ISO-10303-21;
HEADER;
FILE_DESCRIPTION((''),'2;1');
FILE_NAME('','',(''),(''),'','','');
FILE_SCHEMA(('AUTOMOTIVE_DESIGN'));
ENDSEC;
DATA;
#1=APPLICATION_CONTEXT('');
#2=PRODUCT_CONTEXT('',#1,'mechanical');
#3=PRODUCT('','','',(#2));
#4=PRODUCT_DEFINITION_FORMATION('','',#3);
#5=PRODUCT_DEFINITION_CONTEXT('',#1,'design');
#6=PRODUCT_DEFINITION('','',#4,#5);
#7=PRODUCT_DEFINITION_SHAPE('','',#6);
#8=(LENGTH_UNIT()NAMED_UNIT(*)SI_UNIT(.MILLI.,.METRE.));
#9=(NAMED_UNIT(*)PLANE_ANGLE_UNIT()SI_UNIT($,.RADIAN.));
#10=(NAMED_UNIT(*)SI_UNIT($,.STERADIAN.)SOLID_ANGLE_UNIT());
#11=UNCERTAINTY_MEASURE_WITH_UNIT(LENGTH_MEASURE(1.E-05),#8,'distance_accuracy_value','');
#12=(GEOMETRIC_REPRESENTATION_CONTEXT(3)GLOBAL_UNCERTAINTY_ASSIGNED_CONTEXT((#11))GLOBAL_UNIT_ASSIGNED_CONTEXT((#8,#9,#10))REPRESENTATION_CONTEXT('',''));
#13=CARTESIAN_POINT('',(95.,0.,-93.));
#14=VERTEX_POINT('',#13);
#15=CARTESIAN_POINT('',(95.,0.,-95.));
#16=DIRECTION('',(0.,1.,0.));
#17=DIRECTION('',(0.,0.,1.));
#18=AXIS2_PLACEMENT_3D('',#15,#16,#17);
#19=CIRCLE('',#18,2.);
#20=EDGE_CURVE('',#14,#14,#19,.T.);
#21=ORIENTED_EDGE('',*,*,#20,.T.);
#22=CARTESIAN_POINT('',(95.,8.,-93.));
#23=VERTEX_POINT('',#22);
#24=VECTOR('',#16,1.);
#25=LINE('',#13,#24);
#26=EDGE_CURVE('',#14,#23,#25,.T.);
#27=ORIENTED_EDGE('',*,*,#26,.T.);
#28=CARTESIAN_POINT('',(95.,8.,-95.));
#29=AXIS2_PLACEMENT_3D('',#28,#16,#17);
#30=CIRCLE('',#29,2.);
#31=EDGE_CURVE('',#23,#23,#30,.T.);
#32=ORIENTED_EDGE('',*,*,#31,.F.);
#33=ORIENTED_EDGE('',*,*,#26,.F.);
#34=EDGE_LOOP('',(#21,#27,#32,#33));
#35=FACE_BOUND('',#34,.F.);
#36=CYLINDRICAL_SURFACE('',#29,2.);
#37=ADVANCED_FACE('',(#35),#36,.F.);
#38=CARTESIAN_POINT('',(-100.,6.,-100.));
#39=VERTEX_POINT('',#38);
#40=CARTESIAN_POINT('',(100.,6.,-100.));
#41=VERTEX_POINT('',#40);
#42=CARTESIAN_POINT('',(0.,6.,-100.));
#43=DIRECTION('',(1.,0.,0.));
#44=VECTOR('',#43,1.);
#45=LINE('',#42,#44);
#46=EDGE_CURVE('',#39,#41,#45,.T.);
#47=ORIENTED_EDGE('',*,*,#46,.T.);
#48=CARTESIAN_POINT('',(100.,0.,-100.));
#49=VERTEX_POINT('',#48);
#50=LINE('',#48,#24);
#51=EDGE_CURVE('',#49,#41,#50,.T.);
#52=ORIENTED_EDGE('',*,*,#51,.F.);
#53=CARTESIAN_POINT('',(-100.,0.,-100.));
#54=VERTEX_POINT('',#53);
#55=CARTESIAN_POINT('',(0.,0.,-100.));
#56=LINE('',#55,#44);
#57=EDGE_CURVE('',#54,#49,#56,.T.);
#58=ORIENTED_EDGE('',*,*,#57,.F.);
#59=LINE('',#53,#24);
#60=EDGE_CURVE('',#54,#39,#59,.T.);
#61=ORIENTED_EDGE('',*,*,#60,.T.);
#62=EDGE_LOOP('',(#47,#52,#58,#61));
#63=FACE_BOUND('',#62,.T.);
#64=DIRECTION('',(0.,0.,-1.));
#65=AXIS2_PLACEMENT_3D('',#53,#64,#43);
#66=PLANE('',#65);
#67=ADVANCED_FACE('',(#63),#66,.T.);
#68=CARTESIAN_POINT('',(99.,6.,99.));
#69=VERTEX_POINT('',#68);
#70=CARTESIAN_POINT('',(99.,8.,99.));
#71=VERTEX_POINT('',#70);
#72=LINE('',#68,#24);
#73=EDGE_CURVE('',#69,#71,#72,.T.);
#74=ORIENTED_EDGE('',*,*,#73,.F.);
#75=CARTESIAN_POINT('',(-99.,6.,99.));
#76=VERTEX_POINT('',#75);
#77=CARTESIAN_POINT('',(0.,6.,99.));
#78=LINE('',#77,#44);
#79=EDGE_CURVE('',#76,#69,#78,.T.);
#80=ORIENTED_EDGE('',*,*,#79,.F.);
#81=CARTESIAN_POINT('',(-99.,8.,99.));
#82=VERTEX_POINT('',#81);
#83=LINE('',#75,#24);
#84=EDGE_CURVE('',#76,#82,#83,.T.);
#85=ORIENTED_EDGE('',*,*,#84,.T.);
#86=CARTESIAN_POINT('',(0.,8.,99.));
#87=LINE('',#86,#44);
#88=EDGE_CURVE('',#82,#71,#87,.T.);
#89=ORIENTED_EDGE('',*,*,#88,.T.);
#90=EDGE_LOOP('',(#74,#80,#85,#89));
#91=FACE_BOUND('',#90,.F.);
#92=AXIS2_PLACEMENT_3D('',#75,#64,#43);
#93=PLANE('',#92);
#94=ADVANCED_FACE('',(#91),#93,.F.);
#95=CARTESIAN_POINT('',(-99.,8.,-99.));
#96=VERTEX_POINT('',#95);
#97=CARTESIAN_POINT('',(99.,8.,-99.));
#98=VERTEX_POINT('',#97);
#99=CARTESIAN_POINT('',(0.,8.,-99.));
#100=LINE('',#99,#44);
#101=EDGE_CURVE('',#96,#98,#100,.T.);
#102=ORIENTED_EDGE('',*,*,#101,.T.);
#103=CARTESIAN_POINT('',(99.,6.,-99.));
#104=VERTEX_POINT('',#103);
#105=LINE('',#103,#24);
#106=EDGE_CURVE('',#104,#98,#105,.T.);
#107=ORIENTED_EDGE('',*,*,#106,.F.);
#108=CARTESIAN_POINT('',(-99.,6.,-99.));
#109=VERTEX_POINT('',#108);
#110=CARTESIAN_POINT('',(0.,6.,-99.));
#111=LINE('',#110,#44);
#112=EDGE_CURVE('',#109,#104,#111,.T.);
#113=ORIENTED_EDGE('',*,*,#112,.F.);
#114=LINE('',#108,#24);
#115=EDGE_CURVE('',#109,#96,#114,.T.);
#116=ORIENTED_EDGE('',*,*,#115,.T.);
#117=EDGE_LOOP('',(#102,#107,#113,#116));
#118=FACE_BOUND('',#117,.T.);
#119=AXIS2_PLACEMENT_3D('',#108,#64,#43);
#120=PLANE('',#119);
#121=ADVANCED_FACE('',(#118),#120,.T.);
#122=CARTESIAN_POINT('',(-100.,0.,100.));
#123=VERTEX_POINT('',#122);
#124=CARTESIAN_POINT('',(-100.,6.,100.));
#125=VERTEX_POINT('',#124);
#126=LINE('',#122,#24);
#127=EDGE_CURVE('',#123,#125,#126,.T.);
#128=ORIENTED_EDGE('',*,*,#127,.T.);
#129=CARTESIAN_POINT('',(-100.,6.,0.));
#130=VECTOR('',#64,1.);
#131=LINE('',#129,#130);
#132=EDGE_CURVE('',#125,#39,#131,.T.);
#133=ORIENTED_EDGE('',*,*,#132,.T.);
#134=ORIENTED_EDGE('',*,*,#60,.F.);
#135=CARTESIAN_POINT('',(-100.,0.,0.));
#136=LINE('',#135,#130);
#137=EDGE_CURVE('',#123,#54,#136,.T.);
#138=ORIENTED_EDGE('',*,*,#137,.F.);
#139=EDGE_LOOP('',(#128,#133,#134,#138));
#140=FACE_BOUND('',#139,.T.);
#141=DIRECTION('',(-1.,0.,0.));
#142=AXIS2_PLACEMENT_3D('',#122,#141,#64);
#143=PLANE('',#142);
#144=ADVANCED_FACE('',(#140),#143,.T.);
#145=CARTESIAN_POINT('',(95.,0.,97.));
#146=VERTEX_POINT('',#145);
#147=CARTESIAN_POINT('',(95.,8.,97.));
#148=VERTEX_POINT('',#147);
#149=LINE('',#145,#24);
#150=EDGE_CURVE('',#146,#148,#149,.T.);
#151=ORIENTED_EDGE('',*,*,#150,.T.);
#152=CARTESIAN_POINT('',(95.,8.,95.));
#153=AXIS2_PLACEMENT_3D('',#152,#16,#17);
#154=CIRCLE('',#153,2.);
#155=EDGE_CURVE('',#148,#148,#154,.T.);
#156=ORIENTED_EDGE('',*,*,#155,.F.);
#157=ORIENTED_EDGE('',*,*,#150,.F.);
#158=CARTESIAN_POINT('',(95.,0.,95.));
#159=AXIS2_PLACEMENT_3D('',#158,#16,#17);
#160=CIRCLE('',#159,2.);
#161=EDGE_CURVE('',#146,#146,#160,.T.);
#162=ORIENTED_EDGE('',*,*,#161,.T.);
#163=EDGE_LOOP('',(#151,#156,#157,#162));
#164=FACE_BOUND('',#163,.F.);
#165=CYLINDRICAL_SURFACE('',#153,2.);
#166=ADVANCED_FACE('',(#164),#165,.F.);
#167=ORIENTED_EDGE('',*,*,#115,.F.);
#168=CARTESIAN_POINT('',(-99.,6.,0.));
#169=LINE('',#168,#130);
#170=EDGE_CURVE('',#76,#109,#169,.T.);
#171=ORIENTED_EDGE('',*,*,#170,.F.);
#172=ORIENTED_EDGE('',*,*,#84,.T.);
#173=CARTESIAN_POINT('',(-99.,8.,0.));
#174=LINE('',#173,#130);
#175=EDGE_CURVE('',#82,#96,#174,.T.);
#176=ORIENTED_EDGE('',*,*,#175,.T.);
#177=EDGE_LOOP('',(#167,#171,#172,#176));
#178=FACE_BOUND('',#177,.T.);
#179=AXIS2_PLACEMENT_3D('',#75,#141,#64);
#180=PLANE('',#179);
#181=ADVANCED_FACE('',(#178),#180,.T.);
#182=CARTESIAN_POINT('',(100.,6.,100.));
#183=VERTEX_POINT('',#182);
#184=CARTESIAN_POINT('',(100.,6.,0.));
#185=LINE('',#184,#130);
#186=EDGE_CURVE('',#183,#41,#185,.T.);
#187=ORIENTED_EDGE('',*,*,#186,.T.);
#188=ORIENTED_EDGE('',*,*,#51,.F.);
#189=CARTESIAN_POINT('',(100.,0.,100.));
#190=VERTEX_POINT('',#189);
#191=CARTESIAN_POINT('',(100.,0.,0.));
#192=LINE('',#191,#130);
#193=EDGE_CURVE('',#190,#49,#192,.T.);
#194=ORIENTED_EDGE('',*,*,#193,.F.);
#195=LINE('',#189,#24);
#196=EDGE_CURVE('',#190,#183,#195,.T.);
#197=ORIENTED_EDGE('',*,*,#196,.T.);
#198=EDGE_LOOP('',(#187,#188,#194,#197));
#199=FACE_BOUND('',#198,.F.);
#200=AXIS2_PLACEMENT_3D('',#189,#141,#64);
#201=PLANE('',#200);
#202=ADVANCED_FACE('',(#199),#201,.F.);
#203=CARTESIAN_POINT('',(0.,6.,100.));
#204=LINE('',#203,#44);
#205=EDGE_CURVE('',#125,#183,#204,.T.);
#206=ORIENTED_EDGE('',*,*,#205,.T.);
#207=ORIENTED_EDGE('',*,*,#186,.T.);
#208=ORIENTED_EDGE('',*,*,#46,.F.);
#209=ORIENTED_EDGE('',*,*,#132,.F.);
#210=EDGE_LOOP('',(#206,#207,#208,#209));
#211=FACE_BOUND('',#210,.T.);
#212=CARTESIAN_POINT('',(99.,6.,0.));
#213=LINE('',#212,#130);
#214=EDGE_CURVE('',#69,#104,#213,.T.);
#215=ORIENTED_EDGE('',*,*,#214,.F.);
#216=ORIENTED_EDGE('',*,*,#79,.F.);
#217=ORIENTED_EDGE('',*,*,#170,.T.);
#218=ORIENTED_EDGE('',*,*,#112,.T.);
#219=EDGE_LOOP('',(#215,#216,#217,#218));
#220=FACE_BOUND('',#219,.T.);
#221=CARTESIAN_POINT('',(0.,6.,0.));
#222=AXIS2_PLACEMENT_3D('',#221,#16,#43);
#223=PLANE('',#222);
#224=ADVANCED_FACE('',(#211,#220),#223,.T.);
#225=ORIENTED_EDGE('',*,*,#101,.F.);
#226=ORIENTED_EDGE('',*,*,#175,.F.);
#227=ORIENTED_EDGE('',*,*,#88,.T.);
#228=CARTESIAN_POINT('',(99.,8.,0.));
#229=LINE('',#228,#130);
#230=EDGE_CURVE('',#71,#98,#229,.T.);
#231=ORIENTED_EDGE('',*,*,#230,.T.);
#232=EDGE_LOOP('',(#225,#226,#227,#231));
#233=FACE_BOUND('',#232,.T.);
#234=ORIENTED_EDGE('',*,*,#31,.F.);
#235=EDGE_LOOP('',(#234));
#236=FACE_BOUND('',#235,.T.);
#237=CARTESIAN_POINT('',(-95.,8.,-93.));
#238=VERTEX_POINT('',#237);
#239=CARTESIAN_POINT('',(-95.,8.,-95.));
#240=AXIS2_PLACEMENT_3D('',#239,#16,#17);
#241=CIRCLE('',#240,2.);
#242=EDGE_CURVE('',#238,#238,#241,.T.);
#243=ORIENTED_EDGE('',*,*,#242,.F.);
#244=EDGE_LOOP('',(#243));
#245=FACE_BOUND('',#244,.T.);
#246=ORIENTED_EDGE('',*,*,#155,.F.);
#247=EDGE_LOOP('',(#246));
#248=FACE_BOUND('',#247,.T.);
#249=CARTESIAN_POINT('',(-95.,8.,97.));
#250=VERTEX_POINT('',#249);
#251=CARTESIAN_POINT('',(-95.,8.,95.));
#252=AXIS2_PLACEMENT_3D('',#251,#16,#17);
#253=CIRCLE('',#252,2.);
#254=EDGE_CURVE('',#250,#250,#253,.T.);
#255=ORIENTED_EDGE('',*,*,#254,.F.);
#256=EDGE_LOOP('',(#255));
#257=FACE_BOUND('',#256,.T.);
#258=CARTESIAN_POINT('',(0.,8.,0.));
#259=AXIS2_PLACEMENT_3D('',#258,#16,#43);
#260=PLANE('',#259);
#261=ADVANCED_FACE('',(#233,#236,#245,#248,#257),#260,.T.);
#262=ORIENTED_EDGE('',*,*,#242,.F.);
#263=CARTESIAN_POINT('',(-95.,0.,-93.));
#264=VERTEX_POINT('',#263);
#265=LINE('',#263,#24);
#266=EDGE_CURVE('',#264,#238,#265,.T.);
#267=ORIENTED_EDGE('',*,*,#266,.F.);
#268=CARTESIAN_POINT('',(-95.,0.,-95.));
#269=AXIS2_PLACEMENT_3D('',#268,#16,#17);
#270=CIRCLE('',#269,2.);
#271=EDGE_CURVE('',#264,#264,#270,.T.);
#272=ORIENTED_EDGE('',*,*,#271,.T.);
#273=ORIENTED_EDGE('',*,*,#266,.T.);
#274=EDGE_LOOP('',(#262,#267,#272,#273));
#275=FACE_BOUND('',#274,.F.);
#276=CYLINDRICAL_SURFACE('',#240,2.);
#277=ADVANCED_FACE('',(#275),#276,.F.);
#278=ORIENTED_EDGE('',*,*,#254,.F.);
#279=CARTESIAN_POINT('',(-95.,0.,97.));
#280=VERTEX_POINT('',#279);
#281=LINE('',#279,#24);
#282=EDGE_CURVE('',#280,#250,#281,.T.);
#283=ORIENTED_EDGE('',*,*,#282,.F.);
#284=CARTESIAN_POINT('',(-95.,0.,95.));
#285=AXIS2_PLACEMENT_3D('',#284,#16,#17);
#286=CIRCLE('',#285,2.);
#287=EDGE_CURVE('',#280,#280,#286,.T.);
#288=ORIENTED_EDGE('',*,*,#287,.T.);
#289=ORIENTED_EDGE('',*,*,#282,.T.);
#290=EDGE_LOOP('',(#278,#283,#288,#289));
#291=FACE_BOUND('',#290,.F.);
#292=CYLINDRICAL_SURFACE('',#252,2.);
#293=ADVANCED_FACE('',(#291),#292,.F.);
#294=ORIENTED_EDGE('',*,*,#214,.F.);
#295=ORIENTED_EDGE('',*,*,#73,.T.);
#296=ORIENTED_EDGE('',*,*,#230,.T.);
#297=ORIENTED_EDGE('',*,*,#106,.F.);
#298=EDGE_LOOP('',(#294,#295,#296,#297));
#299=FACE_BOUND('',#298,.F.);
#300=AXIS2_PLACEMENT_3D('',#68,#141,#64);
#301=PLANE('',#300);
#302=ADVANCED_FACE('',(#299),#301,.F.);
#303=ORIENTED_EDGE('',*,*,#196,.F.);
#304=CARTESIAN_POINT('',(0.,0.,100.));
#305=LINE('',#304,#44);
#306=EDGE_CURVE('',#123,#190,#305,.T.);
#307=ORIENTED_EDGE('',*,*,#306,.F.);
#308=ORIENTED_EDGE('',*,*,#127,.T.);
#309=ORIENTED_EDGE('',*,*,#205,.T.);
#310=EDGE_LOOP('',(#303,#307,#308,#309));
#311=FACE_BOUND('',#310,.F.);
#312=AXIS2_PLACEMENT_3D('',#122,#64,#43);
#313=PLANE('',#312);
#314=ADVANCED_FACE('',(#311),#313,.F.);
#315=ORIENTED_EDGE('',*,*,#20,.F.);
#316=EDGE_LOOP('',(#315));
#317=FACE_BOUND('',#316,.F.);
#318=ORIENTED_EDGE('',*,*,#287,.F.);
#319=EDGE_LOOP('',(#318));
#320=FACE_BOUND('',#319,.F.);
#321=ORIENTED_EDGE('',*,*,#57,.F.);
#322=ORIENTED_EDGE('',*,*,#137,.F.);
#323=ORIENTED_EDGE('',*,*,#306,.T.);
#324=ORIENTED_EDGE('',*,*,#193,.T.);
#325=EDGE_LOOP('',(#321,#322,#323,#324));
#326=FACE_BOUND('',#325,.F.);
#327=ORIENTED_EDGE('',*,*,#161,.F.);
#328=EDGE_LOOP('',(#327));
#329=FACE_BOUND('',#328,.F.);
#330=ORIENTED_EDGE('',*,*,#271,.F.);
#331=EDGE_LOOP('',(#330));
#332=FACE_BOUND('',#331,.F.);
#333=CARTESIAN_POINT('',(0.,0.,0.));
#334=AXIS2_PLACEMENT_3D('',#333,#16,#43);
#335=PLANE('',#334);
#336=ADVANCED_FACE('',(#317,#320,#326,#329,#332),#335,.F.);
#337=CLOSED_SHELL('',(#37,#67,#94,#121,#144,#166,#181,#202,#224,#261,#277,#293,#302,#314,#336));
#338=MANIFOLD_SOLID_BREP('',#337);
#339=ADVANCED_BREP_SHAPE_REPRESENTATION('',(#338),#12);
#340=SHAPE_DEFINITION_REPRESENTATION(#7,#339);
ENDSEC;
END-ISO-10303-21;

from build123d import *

# Parameters (mm, degrees)
SKETCH1_W           = 200
SKETCH1_H           = 200
SKETCH1_R           = 2
BOSS_EXTRUDE1_DEPTH = 6
SKETCH2_W           = 198
SKETCH2_H           = 198
BOSS_EXTRUDE2_DEPTH = 2
SKETCH4_R           = 2
CUT_EXTRUDE1_DEPTH  = 142.647449677


with BuildPart() as part:
    # Sketch1 → Boss-Extrude1 (new body)
    with BuildSketch(Plane(origin=(0, 0, 0), x_dir=(1, 0, 0), z_dir=(0, 1, 0))):
        Rectangle(SKETCH1_W, SKETCH1_H)
        with Locations(Location((95, 95, 0), (0, 0, 270))):
            Circle(SKETCH1_R, mode=Mode.SUBTRACT)
        with Locations(Location((95, -95, 0), (0, 0, 270))):
            Circle(SKETCH1_R, mode=Mode.SUBTRACT)
        with Locations(Location((-95, -95, 0), (0, 0, 270))):
            Circle(SKETCH1_R, mode=Mode.SUBTRACT)
        with Locations(Location((-95, 95, 0), (0, 0, 270))):
            Circle(SKETCH1_R, mode=Mode.SUBTRACT)
    extrude(amount=BOSS_EXTRUDE1_DEPTH)

    # Sketch2 → Boss-Extrude2 (add)
    with BuildSketch(Plane(origin=(0, 6, 0), x_dir=(1, 0, 0), z_dir=(0, 1, 0))):
        Rectangle(SKETCH2_W, SKETCH2_H)
    extrude(amount=BOSS_EXTRUDE2_DEPTH)

    # Sketch4 → Cut-Extrude1 (cut, through all)
    with BuildSketch(Plane(origin=(0, 8, 0), x_dir=(1, 0, 0), z_dir=(0, 1, 0))):
        with Locations(Location((-95, -95, 0), (0, 0, 270))):
            Circle(SKETCH4_R)
        with Locations(Location((95, -95, 0), (0, 0, 270))):
            Circle(SKETCH4_R)
        with Locations(Location((95, 95, 0), (0, 0, 270))):
            Circle(SKETCH4_R)
        with Locations(Location((-95, 95, 0), (0, 0, 270))):
            Circle(SKETCH4_R)
    extrude(amount=-CUT_EXTRUDE1_DEPTH, mode=Mode.SUBTRACT)


solid = part.part
